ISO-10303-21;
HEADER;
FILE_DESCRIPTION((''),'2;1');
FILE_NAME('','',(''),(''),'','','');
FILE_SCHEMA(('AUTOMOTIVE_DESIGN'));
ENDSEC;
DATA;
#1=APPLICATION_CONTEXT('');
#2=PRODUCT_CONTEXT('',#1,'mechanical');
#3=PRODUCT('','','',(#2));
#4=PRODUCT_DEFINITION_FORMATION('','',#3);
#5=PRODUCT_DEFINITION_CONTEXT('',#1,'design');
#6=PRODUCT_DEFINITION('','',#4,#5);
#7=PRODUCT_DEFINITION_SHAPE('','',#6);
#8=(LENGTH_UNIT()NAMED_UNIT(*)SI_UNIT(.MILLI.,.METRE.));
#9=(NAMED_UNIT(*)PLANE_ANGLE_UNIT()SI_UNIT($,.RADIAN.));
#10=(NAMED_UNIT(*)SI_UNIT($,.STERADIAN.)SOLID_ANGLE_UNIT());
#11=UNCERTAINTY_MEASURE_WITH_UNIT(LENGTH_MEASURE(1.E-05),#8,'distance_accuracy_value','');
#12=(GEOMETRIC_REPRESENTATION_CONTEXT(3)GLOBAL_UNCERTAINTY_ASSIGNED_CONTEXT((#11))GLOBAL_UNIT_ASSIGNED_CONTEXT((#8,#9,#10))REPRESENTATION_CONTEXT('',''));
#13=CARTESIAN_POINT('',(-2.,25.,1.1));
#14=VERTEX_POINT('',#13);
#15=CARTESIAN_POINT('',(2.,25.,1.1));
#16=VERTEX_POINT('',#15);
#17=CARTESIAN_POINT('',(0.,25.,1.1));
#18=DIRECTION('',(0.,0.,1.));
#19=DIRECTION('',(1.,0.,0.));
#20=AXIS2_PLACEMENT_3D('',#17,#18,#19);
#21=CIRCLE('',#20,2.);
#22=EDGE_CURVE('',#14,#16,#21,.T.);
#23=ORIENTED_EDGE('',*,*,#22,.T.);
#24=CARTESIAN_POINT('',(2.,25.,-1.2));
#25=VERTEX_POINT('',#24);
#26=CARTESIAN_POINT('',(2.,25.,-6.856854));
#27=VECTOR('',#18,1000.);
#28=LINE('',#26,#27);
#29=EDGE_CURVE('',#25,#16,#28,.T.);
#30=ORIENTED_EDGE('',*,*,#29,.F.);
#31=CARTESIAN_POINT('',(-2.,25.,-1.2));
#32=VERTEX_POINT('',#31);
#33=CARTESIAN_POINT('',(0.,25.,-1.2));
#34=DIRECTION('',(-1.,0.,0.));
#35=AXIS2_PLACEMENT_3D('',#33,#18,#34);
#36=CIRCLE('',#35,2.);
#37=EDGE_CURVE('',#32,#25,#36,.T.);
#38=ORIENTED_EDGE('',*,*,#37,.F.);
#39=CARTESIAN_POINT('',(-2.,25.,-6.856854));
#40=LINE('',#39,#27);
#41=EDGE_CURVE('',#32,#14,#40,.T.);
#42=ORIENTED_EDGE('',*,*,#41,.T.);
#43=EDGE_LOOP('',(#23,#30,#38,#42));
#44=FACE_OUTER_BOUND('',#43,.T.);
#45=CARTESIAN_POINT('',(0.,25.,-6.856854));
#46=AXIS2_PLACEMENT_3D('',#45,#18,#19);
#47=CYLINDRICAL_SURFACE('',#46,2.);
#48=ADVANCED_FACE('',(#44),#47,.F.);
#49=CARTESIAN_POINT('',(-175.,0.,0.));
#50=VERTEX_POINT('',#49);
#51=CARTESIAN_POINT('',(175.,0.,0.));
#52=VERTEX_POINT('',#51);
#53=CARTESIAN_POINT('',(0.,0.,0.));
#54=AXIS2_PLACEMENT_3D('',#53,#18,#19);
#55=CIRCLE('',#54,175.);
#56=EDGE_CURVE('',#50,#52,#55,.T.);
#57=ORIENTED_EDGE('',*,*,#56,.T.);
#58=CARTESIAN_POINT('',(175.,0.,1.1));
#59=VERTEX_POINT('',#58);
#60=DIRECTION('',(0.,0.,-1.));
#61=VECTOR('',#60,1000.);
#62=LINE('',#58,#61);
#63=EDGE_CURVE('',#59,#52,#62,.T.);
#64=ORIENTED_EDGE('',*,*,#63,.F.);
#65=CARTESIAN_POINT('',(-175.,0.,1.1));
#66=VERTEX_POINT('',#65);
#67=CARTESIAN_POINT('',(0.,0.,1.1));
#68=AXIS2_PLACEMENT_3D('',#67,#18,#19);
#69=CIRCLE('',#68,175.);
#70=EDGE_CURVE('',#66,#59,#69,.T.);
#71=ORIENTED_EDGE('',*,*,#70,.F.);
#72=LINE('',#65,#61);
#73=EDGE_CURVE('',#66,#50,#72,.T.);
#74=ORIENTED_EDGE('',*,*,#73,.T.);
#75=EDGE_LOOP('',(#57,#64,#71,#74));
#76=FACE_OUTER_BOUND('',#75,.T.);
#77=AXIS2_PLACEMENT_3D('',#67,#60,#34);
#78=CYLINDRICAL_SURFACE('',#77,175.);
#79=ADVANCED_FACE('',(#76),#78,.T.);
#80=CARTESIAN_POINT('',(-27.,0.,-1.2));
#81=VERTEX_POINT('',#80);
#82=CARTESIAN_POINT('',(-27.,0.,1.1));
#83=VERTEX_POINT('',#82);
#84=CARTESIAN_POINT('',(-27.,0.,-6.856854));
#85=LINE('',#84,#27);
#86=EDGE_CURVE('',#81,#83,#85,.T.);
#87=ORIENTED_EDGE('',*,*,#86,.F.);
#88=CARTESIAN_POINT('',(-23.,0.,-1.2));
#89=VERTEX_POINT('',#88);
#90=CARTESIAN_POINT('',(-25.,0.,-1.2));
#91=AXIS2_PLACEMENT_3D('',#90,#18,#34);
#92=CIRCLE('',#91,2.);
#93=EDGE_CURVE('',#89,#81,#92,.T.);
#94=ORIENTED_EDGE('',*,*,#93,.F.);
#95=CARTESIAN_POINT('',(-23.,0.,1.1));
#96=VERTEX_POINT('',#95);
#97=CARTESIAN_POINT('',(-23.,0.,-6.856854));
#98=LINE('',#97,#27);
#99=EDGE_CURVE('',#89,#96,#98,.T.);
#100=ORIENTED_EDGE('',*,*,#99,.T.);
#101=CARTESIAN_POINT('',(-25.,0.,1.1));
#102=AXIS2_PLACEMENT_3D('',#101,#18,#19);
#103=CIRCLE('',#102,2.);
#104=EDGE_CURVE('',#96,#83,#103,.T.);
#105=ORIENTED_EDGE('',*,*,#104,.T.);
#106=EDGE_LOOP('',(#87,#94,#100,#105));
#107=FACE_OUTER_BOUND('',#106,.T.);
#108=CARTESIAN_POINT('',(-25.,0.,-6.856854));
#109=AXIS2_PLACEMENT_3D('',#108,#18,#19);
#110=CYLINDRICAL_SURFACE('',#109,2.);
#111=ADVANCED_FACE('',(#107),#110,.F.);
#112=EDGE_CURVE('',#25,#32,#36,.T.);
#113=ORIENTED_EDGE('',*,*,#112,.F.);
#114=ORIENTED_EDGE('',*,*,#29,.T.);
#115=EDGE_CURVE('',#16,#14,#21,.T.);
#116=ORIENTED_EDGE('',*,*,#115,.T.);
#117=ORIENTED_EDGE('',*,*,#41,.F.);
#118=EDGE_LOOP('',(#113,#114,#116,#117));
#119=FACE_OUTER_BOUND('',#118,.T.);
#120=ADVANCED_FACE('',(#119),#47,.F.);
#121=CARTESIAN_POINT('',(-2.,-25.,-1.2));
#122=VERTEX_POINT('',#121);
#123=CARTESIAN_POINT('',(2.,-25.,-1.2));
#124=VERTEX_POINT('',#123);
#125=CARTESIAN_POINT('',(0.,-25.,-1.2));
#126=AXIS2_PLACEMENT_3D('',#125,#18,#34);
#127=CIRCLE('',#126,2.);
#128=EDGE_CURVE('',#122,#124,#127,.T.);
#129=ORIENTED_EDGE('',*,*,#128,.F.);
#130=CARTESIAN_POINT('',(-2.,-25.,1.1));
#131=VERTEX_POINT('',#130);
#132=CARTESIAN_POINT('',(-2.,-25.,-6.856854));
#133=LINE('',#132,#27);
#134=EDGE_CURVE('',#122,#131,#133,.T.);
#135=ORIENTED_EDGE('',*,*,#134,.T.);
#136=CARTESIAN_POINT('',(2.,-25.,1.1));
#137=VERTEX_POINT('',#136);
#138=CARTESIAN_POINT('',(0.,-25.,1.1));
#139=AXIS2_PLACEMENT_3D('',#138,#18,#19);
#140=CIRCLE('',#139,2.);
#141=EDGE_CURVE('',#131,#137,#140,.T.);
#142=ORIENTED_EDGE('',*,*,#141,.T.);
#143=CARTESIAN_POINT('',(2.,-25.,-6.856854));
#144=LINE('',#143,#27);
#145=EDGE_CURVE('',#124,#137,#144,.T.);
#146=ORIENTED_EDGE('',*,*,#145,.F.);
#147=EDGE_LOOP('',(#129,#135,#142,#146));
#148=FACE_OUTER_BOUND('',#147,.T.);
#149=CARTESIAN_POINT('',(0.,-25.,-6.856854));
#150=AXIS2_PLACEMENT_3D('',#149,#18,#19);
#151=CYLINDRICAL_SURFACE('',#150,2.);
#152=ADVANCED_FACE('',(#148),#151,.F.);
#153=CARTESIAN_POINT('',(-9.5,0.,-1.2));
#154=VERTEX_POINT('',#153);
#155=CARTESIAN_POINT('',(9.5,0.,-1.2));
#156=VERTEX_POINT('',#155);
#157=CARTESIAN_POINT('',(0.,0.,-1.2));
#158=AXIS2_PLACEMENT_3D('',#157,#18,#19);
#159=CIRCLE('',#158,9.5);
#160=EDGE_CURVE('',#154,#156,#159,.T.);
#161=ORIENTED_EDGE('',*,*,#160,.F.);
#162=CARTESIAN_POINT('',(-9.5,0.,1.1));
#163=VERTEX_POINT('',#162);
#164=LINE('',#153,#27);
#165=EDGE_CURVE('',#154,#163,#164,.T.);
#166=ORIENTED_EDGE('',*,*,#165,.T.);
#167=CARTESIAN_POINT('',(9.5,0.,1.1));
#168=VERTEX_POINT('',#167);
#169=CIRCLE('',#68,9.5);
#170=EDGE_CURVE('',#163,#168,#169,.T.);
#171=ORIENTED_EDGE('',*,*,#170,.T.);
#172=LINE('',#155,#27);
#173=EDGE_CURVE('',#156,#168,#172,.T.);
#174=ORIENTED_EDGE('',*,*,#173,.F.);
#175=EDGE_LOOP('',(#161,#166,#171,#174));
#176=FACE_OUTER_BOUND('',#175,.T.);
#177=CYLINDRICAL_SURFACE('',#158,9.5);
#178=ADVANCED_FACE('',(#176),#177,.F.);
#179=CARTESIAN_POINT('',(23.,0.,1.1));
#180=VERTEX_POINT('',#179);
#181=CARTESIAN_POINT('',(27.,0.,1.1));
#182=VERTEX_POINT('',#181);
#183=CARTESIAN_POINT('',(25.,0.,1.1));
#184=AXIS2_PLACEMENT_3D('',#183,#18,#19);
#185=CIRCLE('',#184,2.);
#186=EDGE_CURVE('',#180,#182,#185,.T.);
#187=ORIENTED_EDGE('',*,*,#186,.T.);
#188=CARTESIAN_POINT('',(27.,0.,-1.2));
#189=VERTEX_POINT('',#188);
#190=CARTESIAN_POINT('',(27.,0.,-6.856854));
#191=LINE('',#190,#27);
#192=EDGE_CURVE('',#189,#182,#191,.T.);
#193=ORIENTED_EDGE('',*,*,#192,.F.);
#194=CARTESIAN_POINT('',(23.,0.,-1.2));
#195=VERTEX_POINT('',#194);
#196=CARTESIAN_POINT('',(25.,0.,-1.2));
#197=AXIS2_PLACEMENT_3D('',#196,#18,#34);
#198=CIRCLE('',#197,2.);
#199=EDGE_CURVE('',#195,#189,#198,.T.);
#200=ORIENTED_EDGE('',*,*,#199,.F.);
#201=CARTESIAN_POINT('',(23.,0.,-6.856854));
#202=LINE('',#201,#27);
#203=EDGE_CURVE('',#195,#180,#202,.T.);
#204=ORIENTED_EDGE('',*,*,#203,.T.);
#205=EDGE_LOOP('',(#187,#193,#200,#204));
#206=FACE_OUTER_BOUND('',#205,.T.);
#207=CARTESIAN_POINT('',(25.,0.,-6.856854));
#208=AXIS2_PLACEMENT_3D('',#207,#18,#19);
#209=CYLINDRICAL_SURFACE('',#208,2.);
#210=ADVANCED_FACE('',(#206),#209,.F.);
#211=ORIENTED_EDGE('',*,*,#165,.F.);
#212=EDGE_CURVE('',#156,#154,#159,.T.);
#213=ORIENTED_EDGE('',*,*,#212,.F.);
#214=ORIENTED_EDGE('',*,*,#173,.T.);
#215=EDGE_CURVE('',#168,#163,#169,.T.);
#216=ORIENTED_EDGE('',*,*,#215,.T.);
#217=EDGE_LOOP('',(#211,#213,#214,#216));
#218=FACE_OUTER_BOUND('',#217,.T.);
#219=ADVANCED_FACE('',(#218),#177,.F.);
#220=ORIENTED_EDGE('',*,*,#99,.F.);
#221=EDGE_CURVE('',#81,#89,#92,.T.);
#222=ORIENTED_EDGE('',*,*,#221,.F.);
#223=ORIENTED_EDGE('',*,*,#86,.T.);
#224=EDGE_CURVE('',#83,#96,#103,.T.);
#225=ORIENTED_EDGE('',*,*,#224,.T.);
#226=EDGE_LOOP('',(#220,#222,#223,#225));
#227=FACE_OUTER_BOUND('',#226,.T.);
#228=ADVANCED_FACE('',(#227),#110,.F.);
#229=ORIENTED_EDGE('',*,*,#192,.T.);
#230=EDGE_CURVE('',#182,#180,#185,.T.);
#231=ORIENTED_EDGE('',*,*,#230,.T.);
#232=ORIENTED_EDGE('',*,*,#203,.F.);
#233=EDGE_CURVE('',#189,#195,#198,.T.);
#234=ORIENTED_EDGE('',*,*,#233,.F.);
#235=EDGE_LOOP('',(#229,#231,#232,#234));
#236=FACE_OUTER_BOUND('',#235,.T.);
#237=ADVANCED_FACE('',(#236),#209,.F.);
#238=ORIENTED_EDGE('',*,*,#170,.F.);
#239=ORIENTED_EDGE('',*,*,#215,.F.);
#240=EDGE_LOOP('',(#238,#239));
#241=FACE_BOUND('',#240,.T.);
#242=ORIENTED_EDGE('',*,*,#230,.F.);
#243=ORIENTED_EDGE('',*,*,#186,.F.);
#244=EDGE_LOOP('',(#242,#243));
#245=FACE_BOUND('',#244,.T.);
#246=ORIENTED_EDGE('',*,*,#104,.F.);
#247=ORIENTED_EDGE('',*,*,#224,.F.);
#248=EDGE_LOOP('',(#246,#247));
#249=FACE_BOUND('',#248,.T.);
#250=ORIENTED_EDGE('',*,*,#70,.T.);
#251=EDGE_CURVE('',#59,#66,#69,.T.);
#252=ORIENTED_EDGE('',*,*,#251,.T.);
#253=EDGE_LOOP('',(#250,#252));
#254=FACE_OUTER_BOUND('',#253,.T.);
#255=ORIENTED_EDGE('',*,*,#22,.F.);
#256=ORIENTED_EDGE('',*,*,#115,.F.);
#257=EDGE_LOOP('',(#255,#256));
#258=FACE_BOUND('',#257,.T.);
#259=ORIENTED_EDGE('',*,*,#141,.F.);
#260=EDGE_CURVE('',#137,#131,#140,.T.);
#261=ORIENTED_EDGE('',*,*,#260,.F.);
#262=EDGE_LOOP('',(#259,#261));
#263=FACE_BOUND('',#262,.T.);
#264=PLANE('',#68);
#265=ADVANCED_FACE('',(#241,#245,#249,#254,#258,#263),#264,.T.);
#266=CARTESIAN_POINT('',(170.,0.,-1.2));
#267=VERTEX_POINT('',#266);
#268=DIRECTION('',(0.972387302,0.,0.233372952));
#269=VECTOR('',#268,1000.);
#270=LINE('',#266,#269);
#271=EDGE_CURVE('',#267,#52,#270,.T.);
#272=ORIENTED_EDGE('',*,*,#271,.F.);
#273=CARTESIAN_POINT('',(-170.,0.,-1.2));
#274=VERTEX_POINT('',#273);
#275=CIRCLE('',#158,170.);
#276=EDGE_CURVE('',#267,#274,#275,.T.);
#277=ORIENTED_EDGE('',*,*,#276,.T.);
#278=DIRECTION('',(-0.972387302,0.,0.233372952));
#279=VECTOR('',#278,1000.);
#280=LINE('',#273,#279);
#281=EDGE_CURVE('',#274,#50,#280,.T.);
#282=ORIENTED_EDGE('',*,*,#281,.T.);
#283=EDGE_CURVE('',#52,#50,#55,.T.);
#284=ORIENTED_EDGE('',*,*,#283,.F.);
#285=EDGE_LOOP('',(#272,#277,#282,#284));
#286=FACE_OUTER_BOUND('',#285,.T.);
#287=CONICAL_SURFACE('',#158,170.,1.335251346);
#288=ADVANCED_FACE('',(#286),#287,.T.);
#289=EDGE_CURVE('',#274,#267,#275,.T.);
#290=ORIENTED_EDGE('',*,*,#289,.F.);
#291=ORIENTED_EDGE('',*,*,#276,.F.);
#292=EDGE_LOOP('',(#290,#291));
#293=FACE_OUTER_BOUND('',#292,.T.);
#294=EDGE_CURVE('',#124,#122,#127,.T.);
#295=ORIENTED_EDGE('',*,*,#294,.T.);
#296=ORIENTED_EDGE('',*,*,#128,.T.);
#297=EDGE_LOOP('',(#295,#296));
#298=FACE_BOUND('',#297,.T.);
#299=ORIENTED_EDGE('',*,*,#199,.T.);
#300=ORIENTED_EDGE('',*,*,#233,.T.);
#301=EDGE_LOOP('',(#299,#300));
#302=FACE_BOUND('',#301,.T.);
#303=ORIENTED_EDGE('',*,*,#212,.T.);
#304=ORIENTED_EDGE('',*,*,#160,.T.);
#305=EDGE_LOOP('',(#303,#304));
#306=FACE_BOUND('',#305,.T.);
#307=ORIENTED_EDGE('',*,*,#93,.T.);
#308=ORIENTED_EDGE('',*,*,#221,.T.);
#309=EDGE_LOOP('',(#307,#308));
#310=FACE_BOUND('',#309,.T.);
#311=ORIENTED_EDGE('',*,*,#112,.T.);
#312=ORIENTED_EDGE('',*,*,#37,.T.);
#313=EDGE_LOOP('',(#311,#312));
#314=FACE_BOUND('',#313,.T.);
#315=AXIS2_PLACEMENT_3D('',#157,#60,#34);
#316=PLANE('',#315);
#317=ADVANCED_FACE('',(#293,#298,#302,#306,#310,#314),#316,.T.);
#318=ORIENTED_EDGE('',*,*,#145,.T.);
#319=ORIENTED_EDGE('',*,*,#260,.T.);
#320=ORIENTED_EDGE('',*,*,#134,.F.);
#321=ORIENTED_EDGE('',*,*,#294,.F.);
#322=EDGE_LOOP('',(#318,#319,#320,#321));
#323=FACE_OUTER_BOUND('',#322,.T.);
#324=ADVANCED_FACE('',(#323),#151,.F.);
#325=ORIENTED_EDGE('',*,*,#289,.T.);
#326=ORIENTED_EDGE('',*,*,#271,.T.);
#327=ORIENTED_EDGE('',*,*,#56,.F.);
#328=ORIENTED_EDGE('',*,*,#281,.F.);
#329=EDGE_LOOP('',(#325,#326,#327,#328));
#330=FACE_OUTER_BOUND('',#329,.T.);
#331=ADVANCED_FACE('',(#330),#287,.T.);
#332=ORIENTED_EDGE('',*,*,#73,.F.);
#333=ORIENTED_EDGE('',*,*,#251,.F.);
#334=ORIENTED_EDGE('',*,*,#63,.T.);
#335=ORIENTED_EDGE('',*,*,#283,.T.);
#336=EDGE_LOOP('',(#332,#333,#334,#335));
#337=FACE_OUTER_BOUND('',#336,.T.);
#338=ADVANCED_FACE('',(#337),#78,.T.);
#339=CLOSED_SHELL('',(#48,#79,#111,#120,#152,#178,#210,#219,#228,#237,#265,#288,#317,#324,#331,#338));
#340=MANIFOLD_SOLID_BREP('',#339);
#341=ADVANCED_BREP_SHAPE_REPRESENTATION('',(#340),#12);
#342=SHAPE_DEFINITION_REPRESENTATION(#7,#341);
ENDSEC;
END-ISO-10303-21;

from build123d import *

# Parameters (mm, degrees)
SKETCH_3_R          = 175
EXTRUDE_1_DEPTH     = 1.1
SKETCH_4_R          = 170
EXTRUDE_2_DEPTH     = 1.2
SKETCH_7_R          = 9.5
CUT_EXTRUDE_1_DEPTH = 248.498060598
SKETCH_10_R         = 2
CUT_EXTRUDE_2_DEPTH = 2.3


with BuildPart() as part:
    # 草图3 → 凸台-拉伸1 (new body)
    with BuildSketch(Plane.XY):
        Circle(SKETCH_3_R)
    extrude(amount=EXTRUDE_1_DEPTH)

    # 草图4 → 凸台-拉伸2 (add)
    with BuildSketch(Plane(origin=(0, 0, 0), x_dir=(-1, 0, 0), z_dir=(0, 0, -1))):
        with Locations(Location((0, 0, 0), (0, 0, 180))):
            Circle(SKETCH_4_R)
    extrude(amount=EXTRUDE_2_DEPTH)

    # 草图7 → 切除-拉伸1 (cut, through all)
    with BuildSketch(Plane.XY.offset(1.1)):
        Circle(SKETCH_7_R)
    extrude(amount=-CUT_EXTRUDE_1_DEPTH, mode=Mode.SUBTRACT)

    # 扫描1: sweep along a path in 草图9
    with BuildLine(Plane(origin=(0, 0, 0), x_dir=(-1, 0, 0), z_dir=(0, 0, -1))) as sweep_1_path:
        CenterArc((0, 0), 170, 0, 360)
    # 草图8 → 扫描1 (sweep)
    with BuildSketch(Plane(origin=(0, 0, 0), x_dir=(1, 0, 0), z_dir=(0, 1, 0))):
        Polygon((-175, 0), (-170, 1.2), (-170, 0), align=None)
    sweep(path=sweep_1_path.line)

    # 草图10 → 切除-拉伸2 (cut)
    with BuildSketch(Plane.XY.offset(1.1)):
        with Locations((0, 25)):
            Circle(SKETCH_10_R)
        with Locations((25, 0)):
            Circle(SKETCH_10_R)
        with Locations((0, -25)):
            Circle(SKETCH_10_R)
        with Locations((-25, 0)):
            Circle(SKETCH_10_R)
    extrude(amount=-CUT_EXTRUDE_2_DEPTH, mode=Mode.SUBTRACT)


solid = part.part
